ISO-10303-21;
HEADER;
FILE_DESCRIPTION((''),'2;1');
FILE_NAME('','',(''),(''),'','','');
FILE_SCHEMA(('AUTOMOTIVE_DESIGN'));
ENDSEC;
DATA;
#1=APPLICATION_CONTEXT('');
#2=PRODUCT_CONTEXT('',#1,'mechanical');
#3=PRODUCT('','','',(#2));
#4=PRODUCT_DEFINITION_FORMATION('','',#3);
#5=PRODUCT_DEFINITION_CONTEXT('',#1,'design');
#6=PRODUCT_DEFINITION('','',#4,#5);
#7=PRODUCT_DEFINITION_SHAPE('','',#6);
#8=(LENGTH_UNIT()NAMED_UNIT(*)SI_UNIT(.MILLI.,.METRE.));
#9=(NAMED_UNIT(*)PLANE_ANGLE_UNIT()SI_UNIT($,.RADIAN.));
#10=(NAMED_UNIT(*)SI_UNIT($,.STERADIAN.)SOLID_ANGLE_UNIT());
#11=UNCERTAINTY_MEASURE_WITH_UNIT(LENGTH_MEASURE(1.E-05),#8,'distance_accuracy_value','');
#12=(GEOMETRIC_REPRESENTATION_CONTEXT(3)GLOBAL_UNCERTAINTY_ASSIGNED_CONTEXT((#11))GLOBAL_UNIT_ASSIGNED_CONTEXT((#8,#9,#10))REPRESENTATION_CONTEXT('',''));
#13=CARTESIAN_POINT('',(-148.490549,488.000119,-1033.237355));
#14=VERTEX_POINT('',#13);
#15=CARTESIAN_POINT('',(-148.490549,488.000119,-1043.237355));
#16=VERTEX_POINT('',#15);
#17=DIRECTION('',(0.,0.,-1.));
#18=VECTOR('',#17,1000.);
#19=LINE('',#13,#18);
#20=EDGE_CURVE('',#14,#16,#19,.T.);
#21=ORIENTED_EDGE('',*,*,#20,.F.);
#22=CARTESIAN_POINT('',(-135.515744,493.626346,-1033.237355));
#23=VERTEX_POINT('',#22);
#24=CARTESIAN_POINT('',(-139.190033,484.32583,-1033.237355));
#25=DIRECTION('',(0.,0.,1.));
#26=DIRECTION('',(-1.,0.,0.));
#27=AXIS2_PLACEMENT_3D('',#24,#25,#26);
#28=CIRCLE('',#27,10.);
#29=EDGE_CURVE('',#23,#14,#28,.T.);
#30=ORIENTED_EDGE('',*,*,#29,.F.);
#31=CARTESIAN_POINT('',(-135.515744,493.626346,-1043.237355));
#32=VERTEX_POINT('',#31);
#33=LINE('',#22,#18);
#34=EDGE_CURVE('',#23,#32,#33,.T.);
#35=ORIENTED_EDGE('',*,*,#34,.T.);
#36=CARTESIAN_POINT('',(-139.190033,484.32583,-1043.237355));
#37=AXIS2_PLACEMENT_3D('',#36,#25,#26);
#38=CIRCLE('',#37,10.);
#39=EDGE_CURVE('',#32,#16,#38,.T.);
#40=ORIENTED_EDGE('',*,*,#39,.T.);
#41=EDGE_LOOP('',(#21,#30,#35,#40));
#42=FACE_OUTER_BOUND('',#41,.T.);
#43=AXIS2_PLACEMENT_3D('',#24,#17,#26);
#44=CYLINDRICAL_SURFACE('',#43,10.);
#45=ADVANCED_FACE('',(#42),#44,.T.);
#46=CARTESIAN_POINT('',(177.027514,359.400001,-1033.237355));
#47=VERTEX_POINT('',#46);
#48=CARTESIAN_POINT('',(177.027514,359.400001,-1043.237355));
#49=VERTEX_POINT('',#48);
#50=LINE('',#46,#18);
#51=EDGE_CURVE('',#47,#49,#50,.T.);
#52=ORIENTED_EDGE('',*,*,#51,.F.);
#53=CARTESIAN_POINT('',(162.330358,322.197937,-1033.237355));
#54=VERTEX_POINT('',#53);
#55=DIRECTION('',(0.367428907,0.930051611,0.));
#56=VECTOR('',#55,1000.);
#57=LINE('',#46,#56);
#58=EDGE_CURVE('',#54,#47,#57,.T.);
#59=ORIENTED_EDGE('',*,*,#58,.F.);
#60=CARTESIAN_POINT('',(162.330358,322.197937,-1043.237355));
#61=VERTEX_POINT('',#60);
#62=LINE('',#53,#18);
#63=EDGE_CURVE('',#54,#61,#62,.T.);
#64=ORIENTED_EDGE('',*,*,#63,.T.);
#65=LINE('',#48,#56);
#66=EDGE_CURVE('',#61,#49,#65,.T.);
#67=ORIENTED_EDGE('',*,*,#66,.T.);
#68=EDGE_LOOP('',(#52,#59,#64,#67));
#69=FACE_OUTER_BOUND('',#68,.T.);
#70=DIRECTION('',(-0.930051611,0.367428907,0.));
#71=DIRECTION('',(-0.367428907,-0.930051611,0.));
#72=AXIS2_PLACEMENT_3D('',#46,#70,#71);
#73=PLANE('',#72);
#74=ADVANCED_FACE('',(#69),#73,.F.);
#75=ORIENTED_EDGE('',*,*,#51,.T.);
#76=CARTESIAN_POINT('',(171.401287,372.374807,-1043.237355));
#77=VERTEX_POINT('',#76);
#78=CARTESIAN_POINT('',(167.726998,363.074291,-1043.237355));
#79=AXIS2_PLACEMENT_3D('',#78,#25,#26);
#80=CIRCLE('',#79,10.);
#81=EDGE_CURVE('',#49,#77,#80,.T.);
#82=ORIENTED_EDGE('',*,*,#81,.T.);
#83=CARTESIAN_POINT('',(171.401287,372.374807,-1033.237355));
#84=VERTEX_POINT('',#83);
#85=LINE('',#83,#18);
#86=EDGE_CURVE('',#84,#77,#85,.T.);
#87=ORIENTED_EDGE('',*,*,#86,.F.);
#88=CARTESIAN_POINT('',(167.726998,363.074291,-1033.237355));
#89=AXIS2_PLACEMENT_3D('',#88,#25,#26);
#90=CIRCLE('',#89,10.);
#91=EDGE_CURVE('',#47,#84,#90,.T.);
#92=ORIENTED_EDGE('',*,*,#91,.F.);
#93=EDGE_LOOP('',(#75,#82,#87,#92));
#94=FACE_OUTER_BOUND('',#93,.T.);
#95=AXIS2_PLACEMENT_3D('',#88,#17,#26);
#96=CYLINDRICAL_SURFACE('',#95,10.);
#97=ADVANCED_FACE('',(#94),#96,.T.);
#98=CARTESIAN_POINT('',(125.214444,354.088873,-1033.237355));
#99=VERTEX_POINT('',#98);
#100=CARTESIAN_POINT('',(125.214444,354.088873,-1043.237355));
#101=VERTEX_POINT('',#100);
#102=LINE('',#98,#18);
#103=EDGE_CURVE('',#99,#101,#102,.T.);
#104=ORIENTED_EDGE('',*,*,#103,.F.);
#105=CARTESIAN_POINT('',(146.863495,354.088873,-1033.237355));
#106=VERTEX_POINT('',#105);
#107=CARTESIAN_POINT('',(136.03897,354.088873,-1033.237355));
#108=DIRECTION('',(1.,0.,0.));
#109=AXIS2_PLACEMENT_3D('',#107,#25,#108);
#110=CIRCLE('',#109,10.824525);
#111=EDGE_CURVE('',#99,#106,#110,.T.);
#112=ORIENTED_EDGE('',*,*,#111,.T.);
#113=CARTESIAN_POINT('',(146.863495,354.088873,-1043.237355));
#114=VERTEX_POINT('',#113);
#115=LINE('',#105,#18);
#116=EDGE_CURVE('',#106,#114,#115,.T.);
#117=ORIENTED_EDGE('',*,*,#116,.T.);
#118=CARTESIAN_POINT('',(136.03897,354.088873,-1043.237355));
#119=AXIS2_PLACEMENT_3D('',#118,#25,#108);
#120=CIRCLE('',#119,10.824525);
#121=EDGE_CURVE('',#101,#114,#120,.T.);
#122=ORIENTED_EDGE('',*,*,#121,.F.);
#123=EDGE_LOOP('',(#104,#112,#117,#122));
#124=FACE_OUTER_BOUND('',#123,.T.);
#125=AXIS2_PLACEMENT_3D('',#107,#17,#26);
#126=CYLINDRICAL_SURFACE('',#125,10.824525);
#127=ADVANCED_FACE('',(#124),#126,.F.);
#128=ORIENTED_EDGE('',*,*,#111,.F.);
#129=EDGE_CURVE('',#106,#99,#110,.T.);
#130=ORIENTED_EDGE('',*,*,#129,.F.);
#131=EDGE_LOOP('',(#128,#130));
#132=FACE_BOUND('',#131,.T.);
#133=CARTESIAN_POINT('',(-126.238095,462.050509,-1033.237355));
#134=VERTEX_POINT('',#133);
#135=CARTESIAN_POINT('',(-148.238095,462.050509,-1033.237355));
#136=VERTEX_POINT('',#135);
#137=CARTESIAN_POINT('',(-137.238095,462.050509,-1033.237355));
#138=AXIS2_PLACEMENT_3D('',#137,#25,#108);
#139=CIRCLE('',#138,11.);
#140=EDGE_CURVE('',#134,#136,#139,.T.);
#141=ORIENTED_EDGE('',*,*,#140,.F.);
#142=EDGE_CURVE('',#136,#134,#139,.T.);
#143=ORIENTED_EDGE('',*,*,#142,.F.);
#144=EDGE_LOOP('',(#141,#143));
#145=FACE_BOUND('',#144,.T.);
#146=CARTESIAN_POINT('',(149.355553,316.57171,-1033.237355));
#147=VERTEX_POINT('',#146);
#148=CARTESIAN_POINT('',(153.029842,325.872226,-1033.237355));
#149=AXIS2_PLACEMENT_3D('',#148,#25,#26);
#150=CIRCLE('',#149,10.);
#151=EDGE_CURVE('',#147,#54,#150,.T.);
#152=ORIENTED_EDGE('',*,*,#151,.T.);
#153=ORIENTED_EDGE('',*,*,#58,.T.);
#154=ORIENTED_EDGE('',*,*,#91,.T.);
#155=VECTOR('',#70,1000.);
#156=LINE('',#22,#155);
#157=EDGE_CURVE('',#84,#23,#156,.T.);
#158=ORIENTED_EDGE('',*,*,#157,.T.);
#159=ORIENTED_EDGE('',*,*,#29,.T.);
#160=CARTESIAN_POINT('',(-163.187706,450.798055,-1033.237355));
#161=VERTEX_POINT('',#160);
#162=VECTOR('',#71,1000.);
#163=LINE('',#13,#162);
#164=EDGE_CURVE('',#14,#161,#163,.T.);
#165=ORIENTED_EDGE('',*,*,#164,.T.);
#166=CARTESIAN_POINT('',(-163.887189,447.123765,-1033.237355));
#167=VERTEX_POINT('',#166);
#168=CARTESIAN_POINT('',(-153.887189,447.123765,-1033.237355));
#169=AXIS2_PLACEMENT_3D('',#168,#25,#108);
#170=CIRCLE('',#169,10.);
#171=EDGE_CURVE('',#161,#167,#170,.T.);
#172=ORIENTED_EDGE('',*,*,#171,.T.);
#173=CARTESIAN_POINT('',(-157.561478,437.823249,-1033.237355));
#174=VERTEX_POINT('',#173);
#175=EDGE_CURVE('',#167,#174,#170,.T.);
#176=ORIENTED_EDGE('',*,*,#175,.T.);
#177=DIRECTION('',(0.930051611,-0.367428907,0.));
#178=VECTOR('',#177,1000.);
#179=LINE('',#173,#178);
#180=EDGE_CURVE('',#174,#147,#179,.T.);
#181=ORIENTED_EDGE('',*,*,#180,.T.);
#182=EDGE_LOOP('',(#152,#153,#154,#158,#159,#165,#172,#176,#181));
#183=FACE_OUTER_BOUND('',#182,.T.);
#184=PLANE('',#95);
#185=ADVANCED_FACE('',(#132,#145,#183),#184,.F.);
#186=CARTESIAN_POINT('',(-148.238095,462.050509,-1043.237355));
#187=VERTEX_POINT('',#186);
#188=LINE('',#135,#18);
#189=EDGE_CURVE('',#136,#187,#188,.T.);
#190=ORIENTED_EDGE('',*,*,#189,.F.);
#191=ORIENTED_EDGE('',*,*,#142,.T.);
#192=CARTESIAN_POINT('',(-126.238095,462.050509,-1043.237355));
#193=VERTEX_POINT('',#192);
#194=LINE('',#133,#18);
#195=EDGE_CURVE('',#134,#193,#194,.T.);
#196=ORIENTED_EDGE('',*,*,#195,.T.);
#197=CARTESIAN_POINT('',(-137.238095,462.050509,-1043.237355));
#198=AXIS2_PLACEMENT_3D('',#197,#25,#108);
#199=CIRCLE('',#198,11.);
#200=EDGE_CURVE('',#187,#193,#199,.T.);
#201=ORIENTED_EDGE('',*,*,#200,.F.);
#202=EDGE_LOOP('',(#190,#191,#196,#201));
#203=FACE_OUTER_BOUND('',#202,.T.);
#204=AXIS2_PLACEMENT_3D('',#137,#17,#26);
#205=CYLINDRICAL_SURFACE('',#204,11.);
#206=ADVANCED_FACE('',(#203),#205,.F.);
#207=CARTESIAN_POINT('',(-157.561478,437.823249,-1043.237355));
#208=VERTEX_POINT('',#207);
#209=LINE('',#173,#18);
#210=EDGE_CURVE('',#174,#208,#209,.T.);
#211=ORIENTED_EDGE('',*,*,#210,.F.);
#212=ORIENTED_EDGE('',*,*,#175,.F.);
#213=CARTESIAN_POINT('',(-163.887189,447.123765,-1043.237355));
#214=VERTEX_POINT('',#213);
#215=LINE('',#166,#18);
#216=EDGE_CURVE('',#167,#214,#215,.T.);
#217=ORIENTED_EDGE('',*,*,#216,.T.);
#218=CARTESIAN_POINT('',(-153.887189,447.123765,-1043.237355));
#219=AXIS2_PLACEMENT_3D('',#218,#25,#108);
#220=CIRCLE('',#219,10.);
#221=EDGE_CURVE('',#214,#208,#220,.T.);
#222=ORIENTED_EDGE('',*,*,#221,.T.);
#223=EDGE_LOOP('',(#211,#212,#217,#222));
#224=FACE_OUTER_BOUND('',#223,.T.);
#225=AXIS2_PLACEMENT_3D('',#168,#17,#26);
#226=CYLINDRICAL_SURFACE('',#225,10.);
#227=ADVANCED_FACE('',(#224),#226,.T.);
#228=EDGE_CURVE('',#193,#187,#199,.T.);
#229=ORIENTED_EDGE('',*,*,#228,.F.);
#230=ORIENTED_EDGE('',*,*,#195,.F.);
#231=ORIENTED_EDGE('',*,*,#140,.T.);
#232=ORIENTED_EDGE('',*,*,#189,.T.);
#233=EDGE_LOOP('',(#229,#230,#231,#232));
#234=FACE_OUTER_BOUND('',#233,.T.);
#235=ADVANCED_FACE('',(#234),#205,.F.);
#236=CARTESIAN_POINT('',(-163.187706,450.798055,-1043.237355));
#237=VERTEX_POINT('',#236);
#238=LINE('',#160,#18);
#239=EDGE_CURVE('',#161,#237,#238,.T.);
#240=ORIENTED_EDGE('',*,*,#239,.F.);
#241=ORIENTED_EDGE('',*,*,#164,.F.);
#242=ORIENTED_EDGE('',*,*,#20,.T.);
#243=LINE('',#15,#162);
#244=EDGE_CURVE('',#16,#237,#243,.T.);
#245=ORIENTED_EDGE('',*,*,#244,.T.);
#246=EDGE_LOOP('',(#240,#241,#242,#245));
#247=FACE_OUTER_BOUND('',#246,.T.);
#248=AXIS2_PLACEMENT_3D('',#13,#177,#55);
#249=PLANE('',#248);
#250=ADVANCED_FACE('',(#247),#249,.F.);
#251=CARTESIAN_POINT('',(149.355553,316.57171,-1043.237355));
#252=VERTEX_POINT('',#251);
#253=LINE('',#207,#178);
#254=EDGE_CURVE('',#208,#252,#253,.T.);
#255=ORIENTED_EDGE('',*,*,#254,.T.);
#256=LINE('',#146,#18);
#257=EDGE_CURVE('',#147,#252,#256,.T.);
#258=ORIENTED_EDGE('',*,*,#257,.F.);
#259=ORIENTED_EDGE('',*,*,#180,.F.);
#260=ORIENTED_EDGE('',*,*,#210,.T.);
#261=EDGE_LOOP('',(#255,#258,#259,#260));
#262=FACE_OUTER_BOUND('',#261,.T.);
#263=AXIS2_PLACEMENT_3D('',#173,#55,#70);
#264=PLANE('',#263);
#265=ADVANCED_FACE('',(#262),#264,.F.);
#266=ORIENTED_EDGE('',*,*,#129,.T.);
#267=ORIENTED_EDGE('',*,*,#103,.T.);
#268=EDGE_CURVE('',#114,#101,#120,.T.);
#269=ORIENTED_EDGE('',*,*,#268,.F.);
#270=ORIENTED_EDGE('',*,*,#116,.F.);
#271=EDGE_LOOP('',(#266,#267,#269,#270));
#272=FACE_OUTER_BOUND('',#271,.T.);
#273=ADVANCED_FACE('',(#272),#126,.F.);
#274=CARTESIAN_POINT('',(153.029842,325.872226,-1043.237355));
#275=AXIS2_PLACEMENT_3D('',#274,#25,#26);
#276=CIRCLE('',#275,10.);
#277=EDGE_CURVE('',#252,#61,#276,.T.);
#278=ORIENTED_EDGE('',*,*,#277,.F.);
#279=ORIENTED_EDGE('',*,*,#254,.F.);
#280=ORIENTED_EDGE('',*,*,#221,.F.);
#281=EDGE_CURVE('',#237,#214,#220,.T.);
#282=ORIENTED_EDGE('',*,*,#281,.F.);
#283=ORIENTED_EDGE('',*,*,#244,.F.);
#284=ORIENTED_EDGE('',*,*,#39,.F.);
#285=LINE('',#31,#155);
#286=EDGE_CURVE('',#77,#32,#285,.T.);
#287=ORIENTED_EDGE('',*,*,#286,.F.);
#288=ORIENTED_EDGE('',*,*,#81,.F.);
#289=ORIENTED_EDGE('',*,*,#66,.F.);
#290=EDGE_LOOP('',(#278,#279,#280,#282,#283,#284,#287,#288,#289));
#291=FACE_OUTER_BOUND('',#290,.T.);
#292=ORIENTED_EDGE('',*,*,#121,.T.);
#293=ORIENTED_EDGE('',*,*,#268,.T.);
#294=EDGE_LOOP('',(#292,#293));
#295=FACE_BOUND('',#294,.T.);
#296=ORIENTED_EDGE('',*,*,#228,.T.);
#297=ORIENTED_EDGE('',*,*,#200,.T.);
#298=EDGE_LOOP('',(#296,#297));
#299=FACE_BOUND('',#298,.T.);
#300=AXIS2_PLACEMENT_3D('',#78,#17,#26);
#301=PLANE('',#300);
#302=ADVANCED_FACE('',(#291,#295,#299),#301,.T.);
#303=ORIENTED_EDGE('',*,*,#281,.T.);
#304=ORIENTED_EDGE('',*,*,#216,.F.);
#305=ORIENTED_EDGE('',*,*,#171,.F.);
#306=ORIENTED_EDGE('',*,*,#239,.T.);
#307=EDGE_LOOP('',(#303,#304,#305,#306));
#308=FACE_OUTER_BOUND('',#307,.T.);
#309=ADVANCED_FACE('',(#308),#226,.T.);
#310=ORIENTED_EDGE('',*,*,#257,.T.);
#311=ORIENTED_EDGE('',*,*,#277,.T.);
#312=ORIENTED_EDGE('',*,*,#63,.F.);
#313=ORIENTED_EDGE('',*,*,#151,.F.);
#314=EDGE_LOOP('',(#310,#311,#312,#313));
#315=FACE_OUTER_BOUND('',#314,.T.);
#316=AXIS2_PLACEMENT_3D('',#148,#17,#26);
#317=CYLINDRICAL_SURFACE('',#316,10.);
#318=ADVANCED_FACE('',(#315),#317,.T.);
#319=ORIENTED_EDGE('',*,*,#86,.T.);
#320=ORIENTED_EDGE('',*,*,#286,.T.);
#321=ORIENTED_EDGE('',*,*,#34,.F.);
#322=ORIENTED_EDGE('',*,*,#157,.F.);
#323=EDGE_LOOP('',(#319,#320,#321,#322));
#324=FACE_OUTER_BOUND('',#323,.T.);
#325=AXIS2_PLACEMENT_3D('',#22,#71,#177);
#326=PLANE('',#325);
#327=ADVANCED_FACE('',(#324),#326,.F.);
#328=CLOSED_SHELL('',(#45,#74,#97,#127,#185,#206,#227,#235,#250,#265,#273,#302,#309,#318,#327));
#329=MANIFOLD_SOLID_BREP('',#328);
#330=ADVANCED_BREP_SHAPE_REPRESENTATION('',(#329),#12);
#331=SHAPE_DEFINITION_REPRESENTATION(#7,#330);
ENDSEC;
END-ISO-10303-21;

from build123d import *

# Parameters (mm, degrees)
EXTRUDE_START   = 40
SKETCH_1_R      = 11
SKETCH_1_R_2    = 10.824525282
EXTRUDE_1_DEPTH = 10


with BuildPart() as part:
    # 草图1 → 凸台-拉伸1 (new body)
    with BuildSketch(Plane.XY.offset(-1083.237354735).offset(EXTRUDE_START)):
        with BuildLine():
            Line((-135.515744069, 493.626345969), (171.40128741, 372.374806646))
            ThreePointArc((171.40128741, 372.374806646), (176.901571064, 367.052633829), (177.027514445, 359.40000147))
            Line((177.027514445, 359.40000147), (162.330358163, 322.197937048))
            ThreePointArc((162.330358163, 322.197937048), (157.008185347, 316.697653394), (149.355552988, 316.571710013))
            Line((149.355552988, 316.571710013), (-157.561478491, 437.823249336))
            ThreePointArc((-157.561478491, 437.823249336), (-163.061762145, 443.145422153), (-163.187705526, 450.798054512))
            Line((-163.187705526, 450.798054512), (-148.490549245, 488.000118934))
            ThreePointArc((-148.490549245, 488.000118934), (-143.168376428, 493.500402588), (-135.515744069, 493.626345969))
        make_face()
        with Locations((-137.238095175, 462.050508582)):
            Circle(SKETCH_1_R, mode=Mode.SUBTRACT)
        with Locations((136.038969551, 354.088872827)):
            Circle(SKETCH_1_R_2, mode=Mode.SUBTRACT)
    extrude(amount=EXTRUDE_1_DEPTH)


solid = part.part
